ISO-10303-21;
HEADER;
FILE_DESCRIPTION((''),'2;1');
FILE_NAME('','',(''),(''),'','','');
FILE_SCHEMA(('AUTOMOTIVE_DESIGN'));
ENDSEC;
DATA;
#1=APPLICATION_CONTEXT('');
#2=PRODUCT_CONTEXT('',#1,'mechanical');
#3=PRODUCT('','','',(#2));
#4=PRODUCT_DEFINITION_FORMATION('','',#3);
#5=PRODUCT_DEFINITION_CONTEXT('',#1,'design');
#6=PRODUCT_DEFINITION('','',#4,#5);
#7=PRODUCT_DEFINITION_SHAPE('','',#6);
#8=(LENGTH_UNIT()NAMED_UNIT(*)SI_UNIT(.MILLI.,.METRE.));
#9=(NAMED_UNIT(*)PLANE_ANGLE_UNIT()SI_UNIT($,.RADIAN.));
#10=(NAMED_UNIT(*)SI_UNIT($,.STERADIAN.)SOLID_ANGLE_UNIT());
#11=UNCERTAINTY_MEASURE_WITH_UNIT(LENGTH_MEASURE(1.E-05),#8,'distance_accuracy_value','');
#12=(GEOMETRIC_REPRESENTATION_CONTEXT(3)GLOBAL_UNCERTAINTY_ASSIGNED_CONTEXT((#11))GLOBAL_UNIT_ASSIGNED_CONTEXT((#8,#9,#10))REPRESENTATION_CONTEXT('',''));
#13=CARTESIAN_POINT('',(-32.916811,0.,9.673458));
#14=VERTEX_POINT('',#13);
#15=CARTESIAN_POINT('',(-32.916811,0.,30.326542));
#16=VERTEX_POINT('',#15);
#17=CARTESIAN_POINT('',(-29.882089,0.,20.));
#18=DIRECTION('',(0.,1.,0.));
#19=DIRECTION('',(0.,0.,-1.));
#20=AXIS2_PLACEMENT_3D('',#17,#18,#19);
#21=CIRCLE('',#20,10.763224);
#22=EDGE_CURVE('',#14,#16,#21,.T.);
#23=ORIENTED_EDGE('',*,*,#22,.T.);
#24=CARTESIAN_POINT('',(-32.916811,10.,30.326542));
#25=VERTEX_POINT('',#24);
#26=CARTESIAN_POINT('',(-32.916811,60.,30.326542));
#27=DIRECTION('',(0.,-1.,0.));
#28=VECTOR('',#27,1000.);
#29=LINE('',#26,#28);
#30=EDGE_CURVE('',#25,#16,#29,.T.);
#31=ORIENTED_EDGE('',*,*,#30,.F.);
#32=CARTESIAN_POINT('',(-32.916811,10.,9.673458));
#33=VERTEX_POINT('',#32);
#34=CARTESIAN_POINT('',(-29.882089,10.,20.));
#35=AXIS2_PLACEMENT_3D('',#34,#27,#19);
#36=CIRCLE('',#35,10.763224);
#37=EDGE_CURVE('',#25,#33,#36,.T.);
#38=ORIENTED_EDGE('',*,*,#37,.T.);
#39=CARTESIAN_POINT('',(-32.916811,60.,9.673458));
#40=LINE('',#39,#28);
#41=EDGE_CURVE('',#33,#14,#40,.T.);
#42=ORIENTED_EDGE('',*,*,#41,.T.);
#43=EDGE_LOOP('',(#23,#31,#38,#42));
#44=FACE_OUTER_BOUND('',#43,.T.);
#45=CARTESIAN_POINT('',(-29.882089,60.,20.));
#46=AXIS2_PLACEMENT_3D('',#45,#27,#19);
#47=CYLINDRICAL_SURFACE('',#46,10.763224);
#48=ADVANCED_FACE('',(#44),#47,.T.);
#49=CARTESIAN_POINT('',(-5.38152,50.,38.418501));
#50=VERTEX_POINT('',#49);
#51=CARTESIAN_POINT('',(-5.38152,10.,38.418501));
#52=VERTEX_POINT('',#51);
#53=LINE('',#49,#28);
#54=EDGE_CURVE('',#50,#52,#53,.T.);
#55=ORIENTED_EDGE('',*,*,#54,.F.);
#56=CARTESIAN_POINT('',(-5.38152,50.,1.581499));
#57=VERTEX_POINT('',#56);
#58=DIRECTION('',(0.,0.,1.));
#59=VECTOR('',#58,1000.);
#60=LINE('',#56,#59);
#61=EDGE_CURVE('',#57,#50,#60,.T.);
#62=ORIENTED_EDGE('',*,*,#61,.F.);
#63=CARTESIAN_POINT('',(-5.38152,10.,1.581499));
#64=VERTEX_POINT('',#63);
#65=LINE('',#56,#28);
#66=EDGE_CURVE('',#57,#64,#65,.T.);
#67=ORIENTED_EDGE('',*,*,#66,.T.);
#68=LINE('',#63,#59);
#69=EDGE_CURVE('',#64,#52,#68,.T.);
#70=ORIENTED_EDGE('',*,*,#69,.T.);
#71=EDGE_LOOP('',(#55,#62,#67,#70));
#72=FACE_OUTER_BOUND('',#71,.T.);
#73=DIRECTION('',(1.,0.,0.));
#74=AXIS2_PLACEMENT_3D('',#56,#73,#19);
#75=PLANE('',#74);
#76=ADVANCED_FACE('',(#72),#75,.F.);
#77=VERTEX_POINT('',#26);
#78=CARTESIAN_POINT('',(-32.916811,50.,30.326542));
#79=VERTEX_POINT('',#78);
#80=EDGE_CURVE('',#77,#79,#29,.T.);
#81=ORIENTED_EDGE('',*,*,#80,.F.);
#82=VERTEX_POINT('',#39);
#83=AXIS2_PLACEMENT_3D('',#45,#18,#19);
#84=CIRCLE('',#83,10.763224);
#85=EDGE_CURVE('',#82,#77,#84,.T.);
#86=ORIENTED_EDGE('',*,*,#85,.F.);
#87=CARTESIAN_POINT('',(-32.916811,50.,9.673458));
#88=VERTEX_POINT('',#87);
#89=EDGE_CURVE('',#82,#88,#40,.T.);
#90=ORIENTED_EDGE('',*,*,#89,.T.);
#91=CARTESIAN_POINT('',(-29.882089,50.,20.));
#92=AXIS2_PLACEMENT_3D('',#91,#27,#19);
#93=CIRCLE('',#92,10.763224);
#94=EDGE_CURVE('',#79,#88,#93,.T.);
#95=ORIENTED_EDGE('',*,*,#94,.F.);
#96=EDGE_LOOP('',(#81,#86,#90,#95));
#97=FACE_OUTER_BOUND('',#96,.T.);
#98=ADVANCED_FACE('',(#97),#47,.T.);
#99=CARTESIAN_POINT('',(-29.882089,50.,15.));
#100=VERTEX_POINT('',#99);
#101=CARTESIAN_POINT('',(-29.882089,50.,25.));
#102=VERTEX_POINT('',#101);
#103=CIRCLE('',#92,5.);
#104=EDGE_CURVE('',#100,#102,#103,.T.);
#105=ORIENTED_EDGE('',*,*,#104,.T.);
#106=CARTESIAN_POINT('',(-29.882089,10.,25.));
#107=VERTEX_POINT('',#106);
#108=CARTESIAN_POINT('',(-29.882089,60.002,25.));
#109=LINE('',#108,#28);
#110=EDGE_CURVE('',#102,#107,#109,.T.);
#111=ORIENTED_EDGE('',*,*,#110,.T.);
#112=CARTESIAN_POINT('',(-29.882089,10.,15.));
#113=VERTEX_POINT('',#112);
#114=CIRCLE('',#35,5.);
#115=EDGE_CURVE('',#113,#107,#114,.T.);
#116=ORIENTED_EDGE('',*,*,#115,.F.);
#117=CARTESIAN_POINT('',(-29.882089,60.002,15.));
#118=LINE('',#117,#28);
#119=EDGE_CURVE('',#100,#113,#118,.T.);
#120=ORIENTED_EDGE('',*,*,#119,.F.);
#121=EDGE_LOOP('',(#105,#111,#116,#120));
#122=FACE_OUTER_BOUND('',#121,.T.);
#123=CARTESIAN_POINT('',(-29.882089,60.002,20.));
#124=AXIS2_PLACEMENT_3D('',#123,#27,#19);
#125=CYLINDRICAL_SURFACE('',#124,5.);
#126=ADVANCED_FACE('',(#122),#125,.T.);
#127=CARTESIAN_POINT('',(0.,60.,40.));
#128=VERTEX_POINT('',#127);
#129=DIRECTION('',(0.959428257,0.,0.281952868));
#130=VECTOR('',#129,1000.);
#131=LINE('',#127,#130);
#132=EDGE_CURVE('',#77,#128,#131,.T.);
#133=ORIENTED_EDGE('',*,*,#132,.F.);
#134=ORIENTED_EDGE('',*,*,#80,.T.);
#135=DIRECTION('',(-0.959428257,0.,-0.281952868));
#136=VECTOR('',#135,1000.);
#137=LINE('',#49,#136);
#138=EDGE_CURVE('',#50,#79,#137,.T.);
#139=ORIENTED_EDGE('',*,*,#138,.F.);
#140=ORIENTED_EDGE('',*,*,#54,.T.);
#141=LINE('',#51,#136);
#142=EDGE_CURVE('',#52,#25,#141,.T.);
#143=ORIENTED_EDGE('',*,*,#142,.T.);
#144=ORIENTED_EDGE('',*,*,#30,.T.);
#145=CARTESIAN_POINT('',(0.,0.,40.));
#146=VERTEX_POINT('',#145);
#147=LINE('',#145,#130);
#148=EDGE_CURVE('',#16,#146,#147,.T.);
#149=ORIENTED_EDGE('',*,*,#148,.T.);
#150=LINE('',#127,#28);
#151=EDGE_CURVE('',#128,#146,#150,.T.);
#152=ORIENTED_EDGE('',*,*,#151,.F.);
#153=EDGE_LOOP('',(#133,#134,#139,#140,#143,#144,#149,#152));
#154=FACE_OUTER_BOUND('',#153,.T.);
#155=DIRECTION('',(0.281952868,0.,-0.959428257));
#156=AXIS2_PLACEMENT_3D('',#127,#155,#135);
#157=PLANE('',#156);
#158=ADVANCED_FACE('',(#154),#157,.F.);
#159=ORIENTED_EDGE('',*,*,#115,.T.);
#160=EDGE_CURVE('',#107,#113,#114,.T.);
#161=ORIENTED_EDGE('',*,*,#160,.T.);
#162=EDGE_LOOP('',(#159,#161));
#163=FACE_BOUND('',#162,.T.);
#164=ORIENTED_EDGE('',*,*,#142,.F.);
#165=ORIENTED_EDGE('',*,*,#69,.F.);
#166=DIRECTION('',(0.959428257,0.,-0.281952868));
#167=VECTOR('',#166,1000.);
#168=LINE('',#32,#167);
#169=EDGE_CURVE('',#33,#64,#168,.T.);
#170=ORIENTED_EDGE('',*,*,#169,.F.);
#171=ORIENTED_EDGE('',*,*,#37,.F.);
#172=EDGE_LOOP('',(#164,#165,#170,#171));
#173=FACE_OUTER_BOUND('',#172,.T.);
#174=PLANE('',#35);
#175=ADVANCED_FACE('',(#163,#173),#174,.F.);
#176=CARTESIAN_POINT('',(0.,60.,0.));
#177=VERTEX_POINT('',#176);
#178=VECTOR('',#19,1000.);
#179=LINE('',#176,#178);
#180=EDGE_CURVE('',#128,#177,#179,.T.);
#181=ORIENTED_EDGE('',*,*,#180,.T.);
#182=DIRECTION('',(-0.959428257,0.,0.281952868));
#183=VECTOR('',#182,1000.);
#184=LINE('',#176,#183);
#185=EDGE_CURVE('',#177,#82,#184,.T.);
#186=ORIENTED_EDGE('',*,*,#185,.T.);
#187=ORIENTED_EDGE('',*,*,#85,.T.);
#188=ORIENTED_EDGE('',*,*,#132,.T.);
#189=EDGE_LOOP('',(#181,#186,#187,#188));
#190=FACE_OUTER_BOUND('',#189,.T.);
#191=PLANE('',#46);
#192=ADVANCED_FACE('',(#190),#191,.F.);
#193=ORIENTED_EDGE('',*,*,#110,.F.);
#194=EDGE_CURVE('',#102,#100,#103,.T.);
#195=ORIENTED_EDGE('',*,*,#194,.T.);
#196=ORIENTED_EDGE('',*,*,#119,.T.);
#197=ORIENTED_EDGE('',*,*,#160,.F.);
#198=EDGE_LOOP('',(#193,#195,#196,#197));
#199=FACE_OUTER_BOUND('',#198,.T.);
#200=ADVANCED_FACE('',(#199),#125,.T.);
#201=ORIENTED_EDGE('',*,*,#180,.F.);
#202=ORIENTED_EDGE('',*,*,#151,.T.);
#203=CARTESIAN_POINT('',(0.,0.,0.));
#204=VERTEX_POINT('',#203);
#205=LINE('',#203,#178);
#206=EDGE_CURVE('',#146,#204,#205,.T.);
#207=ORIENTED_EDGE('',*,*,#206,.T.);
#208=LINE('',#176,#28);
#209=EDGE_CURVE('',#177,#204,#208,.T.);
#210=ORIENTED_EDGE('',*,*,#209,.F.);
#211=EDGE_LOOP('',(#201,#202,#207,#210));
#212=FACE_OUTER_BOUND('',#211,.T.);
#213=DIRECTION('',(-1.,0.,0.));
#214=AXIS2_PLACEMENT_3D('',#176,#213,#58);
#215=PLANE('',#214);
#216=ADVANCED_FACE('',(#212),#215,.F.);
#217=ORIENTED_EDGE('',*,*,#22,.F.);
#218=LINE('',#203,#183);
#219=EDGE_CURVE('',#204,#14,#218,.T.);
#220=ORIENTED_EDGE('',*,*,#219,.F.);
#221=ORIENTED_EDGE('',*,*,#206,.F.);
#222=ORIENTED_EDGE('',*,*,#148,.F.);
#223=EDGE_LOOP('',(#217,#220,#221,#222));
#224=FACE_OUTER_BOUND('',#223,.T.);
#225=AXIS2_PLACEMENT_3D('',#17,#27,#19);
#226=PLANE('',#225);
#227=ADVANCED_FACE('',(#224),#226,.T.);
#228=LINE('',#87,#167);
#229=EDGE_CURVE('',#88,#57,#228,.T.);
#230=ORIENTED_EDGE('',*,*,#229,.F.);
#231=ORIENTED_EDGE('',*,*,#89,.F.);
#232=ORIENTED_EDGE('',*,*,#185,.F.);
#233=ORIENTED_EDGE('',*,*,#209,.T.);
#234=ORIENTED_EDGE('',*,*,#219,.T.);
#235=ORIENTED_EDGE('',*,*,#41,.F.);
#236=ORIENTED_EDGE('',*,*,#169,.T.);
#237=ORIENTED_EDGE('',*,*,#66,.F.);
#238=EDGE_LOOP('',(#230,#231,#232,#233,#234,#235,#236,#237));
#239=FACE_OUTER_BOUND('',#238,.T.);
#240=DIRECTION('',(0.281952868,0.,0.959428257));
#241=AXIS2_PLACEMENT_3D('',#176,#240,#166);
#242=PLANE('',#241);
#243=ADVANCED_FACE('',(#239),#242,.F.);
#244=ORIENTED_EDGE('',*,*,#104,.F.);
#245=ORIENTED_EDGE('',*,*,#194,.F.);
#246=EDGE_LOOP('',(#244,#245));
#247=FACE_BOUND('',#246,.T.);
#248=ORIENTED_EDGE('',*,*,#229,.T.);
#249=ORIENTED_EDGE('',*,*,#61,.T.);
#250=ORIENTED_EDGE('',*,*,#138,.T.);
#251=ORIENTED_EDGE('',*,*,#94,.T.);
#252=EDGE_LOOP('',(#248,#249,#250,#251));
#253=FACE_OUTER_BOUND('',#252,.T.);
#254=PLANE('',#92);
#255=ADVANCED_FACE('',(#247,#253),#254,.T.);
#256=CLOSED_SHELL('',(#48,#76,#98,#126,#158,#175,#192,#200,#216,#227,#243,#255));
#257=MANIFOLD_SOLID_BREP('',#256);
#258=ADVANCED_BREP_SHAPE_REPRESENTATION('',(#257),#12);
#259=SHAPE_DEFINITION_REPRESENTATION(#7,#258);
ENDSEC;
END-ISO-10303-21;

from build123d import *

# Parameters (mm, degrees)
BOSS_EXTRUDE1_DEPTH = 60
CUT_EXTRUDE1_DEPTH  = 40
BOSS_EXTRUDE2_REACH = 77.842
SKETCH3_R           = 5


with BuildPart() as part:
    # Sketch1 → Boss-Extrude1 (new body)
    with BuildSketch(Plane(origin=(0, 0, 0), x_dir=(1, 0, 0), z_dir=(0, 1, 0))):
        with BuildLine():
            Line((0, 0), (0, -40))
            Line((0, -40), (-32.916811342, -30.326541582))
            ThreePointArc((-32.916811342, -30.326541582), (-40.645313725, -20), (-32.916811342, -9.673458418))
            Line((-32.916811342, -9.673458418), (0, 0))
        make_face()
    extrude(amount=BOSS_EXTRUDE1_DEPTH)

    # Sketch2 → Cut-Extrude1 (cut)
    with BuildSketch(Plane(origin=(0, 10, 0), x_dir=(-1, 0, 0), z_dir=(0, -1, 0))):
        with BuildLine():
            Line((5.381519546, -1.581499041), (5.381519546, -38.418500959))
            Line((5.381519546, -38.418500959), (32.916811342, -30.326541582))
            ThreePointArc((32.916811342, -30.326541582), (40.645313725, -20), (32.916811342, -9.673458418))
            Line((32.916811342, -9.673458418), (5.381519546, -1.581499041))
        make_face()
    extrude(amount=-CUT_EXTRUDE1_DEPTH, mode=Mode.SUBTRACT)

    # Sketch3 → Boss-Extrude2 (add, up to next)
    with BuildSketch(Plane(origin=(0, 10, 0), x_dir=(-1, 0, 0), z_dir=(0, -1, 0)), mode=Mode.PRIVATE) as boss_extrude2_sk1:
        with Locations(Location((29.882089371, -20, 0), (0, 0, 90))):
            Circle(SKETCH3_R)
    boss_extrude2_tool1 = extrude(boss_extrude2_sk1.sketch, amount=-BOSS_EXTRUDE2_REACH, mode=Mode.PRIVATE) - part.part
    add(boss_extrude2_tool1.solids().sort_by_distance((-29.882089, 10, 20))[0])


solid = part.part
